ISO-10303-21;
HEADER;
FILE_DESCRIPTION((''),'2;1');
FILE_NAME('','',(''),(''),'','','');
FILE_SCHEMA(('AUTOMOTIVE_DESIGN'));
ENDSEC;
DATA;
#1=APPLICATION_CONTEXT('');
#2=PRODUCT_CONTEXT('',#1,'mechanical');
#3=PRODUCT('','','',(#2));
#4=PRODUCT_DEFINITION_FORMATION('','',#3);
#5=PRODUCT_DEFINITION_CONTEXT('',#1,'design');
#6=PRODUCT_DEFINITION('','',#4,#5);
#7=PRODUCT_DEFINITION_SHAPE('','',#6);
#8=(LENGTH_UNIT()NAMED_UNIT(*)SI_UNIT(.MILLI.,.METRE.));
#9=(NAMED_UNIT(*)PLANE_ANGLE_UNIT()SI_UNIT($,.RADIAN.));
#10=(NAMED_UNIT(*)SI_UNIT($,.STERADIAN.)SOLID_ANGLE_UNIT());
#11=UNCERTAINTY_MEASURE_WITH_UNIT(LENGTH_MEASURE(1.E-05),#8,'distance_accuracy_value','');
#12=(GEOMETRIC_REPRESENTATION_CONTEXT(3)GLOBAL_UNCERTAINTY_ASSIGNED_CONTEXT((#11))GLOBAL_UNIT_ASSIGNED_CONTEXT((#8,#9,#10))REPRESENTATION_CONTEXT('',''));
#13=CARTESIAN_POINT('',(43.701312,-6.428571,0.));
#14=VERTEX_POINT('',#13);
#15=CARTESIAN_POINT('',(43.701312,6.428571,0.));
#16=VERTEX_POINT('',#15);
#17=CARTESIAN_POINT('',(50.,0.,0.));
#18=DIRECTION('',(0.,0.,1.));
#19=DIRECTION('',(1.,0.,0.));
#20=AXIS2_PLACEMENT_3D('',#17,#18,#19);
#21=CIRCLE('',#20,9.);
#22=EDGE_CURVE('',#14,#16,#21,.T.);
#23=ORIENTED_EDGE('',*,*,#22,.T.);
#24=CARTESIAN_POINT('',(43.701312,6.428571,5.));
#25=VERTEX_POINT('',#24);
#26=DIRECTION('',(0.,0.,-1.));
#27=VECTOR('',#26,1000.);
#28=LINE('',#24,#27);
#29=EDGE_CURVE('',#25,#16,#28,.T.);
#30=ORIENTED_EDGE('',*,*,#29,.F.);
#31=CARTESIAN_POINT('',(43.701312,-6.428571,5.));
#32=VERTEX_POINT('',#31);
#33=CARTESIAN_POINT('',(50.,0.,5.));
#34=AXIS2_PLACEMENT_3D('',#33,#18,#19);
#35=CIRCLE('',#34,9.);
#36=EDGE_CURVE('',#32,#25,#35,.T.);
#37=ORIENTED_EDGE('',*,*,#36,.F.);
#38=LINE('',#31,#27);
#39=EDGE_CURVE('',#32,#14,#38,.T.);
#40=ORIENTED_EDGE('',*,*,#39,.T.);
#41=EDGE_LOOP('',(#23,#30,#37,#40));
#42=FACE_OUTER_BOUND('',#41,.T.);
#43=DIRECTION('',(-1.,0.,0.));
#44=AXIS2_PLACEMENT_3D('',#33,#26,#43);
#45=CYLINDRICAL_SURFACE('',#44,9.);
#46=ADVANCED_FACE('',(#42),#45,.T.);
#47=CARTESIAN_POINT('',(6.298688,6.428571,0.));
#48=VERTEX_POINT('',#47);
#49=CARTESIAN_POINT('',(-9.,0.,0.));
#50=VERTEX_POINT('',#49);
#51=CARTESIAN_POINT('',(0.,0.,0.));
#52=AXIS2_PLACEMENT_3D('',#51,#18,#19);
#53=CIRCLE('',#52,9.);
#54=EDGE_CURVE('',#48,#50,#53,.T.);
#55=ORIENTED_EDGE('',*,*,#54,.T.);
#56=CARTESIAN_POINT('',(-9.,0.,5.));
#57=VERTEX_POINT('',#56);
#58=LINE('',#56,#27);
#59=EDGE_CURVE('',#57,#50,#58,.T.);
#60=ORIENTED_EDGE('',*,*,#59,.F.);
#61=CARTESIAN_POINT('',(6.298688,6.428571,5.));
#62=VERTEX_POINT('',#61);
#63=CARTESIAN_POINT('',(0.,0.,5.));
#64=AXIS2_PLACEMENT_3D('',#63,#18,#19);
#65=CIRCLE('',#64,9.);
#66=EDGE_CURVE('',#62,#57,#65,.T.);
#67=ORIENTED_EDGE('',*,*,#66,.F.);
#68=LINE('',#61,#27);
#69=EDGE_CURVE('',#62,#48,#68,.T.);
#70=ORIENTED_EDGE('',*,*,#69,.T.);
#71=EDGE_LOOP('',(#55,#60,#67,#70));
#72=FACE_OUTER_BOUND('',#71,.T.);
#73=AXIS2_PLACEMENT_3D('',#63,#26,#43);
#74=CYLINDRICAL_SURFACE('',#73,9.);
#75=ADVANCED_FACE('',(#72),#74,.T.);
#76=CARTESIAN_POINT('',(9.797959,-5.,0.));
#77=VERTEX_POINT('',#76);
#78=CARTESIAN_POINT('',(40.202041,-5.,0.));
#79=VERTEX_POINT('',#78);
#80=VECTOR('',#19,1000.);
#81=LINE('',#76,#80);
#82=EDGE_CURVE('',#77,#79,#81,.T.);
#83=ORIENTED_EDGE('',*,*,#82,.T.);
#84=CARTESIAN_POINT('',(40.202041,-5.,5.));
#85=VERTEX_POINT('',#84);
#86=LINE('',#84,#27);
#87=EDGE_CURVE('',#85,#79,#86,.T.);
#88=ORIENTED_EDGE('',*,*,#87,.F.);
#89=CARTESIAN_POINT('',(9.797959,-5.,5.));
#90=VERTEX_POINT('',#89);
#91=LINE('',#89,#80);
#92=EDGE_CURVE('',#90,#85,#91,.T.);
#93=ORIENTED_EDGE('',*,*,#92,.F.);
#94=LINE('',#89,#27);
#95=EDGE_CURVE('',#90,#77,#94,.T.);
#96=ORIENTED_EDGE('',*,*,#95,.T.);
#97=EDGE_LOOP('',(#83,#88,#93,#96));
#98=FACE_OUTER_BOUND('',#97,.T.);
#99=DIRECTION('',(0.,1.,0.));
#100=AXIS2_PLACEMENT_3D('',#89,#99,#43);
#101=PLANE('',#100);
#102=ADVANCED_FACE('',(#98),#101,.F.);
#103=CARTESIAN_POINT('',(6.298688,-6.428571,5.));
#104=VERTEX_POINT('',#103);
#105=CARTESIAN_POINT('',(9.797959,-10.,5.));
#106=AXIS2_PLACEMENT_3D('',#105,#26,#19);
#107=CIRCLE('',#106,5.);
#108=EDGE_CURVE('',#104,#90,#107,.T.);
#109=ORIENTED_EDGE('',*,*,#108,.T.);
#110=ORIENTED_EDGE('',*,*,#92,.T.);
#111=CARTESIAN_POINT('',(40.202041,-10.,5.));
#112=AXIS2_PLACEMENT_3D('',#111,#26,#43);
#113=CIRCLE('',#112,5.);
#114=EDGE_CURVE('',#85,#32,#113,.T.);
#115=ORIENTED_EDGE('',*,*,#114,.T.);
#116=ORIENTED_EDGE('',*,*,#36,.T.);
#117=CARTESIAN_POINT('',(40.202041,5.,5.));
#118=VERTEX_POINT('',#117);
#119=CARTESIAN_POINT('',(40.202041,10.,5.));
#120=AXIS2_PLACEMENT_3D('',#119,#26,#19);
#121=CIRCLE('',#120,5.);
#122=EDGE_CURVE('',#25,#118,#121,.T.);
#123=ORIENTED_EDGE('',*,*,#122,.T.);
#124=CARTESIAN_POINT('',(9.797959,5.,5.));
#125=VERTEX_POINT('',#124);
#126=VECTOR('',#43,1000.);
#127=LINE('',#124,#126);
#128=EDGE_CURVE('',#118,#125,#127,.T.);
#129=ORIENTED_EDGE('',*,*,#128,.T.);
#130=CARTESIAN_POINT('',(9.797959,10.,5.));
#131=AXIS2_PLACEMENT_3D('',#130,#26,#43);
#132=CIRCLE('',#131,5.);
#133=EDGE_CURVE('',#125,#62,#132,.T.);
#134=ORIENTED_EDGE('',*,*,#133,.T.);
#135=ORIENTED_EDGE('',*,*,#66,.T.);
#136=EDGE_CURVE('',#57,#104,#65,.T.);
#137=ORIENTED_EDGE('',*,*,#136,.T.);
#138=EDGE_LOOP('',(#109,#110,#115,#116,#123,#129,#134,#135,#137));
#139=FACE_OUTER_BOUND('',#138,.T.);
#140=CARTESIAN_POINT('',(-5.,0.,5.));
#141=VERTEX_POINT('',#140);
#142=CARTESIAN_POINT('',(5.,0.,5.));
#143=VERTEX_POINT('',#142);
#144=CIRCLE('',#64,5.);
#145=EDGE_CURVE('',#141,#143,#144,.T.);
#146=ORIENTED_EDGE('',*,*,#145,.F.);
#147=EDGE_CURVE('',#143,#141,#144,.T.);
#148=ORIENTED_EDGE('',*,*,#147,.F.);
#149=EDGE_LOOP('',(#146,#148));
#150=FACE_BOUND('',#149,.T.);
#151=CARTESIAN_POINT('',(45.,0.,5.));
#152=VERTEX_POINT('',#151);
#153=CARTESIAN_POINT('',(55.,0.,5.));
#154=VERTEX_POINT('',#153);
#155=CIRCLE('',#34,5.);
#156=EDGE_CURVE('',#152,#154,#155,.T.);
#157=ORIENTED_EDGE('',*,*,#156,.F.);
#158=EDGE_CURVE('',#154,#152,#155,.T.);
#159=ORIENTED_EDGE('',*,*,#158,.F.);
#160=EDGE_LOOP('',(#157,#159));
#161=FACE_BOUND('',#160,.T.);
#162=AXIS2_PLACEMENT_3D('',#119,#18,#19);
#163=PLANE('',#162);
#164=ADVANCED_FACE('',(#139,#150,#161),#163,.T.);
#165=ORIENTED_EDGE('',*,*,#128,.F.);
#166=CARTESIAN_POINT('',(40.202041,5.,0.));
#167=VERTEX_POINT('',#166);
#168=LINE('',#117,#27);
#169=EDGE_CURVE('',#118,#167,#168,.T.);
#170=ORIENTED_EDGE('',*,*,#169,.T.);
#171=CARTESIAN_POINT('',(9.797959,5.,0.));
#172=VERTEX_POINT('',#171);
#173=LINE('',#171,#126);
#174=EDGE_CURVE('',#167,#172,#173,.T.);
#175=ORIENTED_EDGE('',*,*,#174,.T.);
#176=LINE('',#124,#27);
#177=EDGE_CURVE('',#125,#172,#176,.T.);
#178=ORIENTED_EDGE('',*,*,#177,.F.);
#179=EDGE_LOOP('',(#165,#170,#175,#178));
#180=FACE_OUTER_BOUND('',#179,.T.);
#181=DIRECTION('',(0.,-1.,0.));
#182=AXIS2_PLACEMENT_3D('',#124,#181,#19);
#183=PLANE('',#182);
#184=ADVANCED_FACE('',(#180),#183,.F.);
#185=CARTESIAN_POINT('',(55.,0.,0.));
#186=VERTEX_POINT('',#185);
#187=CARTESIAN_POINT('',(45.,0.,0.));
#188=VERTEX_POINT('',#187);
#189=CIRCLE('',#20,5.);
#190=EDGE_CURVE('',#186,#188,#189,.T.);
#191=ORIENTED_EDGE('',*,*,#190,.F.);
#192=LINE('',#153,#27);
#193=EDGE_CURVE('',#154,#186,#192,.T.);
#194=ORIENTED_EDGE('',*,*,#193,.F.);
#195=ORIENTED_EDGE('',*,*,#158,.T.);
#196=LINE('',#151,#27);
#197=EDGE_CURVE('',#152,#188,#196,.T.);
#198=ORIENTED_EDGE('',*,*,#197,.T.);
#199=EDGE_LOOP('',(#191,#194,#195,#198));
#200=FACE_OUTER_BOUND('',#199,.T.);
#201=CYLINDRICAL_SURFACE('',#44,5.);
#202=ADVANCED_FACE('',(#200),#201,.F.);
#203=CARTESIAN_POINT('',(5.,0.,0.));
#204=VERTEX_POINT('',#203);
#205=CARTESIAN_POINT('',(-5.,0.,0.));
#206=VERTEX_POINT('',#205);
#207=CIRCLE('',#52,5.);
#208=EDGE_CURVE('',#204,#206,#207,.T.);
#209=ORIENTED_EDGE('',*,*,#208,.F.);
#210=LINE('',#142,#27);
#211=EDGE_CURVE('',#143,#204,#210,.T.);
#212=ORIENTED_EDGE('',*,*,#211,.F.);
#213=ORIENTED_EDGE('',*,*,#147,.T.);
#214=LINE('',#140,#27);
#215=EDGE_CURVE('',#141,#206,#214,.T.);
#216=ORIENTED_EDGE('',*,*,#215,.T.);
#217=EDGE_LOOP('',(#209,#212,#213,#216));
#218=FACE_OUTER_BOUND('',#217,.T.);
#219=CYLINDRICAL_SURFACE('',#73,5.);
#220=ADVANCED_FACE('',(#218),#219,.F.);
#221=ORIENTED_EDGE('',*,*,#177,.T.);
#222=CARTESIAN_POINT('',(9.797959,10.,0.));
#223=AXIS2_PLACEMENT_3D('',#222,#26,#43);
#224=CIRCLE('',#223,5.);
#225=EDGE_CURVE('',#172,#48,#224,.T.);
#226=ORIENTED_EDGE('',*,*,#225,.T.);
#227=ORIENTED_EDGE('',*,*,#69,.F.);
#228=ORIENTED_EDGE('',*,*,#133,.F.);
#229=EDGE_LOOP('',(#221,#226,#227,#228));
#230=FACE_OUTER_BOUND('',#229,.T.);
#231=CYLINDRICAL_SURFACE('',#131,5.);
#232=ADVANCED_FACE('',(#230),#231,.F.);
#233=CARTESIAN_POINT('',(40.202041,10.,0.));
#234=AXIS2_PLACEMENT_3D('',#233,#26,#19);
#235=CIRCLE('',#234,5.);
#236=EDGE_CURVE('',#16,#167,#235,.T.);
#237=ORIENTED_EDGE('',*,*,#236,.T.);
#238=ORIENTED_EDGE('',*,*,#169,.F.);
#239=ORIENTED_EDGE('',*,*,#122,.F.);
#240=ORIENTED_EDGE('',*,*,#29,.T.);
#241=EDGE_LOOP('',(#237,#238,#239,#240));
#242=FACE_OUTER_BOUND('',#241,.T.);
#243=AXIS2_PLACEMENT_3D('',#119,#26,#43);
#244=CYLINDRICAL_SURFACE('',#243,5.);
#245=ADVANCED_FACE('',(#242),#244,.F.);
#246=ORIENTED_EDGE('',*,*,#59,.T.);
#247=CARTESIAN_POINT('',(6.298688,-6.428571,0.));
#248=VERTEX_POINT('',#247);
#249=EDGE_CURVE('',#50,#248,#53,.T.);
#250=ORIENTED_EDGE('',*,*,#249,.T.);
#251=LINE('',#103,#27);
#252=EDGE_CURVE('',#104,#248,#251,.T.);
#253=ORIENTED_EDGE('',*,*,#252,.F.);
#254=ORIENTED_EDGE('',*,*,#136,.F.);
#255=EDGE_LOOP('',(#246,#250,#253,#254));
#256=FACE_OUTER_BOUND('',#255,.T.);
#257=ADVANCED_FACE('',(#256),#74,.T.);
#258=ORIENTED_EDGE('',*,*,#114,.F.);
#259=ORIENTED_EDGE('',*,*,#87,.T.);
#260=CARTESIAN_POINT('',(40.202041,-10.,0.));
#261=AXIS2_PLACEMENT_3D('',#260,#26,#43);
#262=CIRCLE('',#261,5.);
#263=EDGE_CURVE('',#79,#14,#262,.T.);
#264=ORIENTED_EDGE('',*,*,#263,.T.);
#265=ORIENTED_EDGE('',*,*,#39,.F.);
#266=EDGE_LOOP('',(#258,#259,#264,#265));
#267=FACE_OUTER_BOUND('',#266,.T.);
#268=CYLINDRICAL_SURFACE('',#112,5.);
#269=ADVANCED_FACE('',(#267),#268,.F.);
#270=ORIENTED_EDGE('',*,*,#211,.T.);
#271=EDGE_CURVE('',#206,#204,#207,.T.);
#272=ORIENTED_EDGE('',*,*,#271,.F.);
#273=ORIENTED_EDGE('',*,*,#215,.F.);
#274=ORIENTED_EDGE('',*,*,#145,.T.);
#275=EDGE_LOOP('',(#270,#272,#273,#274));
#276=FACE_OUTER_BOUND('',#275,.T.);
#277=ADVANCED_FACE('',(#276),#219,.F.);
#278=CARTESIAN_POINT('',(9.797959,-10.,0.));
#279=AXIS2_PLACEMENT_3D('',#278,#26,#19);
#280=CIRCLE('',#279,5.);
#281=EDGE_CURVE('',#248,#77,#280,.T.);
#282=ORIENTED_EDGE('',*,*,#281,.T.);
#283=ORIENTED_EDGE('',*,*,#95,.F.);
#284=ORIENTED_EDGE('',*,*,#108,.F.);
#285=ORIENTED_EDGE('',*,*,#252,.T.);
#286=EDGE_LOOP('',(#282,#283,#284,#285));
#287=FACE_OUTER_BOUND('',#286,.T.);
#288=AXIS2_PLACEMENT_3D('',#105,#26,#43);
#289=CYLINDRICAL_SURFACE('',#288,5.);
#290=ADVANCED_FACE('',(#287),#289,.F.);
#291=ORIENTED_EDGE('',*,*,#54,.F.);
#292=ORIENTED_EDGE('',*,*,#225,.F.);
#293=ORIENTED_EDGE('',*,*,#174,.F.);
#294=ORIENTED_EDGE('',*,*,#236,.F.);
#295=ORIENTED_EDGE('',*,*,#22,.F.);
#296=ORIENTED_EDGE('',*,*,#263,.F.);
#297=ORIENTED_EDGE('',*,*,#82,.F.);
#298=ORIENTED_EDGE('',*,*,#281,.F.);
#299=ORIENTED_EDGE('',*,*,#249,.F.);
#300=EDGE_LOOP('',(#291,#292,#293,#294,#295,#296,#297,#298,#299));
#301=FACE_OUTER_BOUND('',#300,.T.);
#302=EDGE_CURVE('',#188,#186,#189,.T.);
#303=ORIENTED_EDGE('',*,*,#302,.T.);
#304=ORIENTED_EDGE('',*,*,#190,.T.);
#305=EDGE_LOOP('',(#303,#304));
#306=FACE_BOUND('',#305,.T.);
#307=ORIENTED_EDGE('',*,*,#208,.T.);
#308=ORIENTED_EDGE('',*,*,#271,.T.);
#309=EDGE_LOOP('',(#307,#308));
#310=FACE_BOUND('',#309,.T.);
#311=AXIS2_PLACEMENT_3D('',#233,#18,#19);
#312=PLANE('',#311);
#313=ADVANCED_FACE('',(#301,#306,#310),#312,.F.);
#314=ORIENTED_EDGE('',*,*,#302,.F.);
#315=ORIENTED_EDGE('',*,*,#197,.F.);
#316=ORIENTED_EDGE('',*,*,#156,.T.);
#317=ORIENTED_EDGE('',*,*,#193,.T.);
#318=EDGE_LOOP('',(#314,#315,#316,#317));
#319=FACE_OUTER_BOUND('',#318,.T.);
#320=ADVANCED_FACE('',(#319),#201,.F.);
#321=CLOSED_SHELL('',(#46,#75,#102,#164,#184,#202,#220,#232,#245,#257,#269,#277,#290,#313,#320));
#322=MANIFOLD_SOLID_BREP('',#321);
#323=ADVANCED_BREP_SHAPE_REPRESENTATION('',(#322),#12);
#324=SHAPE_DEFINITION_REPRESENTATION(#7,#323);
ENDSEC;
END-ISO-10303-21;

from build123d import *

# Parameters (mm, degrees)
SKETCH1_R           = 5
BOSS_EXTRUDE1_DEPTH = 5


with BuildPart() as part:
    # Sketch1 → Boss-Extrude1 (new body)
    with BuildSketch(Plane.XY):
        with BuildLine():
            Line((9.797958971, 5), (40.202041029, 5))
            ThreePointArc((40.202041029, 5), (42.091863394, 5.370899501), (43.70131209, 6.428571429))
            ThreePointArc((43.70131209, 6.428571429), (59, 0), (43.70131209, -6.428571429))
            ThreePointArc((43.70131209, -6.428571429), (42.091863394, -5.370899501), (40.202041029, -5))
            Line((40.202041029, -5), (9.797958971, -5))
            ThreePointArc((9.797958971, -5), (7.908136606, -5.370899501), (6.29868791, -6.428571429))
            ThreePointArc((6.29868791, -6.428571429), (-9, 0), (6.29868791, 6.428571429))
            ThreePointArc((6.29868791, 6.428571429), (7.908136606, 5.370899501), (9.797958971, 5))
        make_face()
        Circle(SKETCH1_R, mode=Mode.SUBTRACT)
        with Locations((50, 0)):
            Circle(SKETCH1_R, mode=Mode.SUBTRACT)
    extrude(amount=BOSS_EXTRUDE1_DEPTH)


solid = part.part
